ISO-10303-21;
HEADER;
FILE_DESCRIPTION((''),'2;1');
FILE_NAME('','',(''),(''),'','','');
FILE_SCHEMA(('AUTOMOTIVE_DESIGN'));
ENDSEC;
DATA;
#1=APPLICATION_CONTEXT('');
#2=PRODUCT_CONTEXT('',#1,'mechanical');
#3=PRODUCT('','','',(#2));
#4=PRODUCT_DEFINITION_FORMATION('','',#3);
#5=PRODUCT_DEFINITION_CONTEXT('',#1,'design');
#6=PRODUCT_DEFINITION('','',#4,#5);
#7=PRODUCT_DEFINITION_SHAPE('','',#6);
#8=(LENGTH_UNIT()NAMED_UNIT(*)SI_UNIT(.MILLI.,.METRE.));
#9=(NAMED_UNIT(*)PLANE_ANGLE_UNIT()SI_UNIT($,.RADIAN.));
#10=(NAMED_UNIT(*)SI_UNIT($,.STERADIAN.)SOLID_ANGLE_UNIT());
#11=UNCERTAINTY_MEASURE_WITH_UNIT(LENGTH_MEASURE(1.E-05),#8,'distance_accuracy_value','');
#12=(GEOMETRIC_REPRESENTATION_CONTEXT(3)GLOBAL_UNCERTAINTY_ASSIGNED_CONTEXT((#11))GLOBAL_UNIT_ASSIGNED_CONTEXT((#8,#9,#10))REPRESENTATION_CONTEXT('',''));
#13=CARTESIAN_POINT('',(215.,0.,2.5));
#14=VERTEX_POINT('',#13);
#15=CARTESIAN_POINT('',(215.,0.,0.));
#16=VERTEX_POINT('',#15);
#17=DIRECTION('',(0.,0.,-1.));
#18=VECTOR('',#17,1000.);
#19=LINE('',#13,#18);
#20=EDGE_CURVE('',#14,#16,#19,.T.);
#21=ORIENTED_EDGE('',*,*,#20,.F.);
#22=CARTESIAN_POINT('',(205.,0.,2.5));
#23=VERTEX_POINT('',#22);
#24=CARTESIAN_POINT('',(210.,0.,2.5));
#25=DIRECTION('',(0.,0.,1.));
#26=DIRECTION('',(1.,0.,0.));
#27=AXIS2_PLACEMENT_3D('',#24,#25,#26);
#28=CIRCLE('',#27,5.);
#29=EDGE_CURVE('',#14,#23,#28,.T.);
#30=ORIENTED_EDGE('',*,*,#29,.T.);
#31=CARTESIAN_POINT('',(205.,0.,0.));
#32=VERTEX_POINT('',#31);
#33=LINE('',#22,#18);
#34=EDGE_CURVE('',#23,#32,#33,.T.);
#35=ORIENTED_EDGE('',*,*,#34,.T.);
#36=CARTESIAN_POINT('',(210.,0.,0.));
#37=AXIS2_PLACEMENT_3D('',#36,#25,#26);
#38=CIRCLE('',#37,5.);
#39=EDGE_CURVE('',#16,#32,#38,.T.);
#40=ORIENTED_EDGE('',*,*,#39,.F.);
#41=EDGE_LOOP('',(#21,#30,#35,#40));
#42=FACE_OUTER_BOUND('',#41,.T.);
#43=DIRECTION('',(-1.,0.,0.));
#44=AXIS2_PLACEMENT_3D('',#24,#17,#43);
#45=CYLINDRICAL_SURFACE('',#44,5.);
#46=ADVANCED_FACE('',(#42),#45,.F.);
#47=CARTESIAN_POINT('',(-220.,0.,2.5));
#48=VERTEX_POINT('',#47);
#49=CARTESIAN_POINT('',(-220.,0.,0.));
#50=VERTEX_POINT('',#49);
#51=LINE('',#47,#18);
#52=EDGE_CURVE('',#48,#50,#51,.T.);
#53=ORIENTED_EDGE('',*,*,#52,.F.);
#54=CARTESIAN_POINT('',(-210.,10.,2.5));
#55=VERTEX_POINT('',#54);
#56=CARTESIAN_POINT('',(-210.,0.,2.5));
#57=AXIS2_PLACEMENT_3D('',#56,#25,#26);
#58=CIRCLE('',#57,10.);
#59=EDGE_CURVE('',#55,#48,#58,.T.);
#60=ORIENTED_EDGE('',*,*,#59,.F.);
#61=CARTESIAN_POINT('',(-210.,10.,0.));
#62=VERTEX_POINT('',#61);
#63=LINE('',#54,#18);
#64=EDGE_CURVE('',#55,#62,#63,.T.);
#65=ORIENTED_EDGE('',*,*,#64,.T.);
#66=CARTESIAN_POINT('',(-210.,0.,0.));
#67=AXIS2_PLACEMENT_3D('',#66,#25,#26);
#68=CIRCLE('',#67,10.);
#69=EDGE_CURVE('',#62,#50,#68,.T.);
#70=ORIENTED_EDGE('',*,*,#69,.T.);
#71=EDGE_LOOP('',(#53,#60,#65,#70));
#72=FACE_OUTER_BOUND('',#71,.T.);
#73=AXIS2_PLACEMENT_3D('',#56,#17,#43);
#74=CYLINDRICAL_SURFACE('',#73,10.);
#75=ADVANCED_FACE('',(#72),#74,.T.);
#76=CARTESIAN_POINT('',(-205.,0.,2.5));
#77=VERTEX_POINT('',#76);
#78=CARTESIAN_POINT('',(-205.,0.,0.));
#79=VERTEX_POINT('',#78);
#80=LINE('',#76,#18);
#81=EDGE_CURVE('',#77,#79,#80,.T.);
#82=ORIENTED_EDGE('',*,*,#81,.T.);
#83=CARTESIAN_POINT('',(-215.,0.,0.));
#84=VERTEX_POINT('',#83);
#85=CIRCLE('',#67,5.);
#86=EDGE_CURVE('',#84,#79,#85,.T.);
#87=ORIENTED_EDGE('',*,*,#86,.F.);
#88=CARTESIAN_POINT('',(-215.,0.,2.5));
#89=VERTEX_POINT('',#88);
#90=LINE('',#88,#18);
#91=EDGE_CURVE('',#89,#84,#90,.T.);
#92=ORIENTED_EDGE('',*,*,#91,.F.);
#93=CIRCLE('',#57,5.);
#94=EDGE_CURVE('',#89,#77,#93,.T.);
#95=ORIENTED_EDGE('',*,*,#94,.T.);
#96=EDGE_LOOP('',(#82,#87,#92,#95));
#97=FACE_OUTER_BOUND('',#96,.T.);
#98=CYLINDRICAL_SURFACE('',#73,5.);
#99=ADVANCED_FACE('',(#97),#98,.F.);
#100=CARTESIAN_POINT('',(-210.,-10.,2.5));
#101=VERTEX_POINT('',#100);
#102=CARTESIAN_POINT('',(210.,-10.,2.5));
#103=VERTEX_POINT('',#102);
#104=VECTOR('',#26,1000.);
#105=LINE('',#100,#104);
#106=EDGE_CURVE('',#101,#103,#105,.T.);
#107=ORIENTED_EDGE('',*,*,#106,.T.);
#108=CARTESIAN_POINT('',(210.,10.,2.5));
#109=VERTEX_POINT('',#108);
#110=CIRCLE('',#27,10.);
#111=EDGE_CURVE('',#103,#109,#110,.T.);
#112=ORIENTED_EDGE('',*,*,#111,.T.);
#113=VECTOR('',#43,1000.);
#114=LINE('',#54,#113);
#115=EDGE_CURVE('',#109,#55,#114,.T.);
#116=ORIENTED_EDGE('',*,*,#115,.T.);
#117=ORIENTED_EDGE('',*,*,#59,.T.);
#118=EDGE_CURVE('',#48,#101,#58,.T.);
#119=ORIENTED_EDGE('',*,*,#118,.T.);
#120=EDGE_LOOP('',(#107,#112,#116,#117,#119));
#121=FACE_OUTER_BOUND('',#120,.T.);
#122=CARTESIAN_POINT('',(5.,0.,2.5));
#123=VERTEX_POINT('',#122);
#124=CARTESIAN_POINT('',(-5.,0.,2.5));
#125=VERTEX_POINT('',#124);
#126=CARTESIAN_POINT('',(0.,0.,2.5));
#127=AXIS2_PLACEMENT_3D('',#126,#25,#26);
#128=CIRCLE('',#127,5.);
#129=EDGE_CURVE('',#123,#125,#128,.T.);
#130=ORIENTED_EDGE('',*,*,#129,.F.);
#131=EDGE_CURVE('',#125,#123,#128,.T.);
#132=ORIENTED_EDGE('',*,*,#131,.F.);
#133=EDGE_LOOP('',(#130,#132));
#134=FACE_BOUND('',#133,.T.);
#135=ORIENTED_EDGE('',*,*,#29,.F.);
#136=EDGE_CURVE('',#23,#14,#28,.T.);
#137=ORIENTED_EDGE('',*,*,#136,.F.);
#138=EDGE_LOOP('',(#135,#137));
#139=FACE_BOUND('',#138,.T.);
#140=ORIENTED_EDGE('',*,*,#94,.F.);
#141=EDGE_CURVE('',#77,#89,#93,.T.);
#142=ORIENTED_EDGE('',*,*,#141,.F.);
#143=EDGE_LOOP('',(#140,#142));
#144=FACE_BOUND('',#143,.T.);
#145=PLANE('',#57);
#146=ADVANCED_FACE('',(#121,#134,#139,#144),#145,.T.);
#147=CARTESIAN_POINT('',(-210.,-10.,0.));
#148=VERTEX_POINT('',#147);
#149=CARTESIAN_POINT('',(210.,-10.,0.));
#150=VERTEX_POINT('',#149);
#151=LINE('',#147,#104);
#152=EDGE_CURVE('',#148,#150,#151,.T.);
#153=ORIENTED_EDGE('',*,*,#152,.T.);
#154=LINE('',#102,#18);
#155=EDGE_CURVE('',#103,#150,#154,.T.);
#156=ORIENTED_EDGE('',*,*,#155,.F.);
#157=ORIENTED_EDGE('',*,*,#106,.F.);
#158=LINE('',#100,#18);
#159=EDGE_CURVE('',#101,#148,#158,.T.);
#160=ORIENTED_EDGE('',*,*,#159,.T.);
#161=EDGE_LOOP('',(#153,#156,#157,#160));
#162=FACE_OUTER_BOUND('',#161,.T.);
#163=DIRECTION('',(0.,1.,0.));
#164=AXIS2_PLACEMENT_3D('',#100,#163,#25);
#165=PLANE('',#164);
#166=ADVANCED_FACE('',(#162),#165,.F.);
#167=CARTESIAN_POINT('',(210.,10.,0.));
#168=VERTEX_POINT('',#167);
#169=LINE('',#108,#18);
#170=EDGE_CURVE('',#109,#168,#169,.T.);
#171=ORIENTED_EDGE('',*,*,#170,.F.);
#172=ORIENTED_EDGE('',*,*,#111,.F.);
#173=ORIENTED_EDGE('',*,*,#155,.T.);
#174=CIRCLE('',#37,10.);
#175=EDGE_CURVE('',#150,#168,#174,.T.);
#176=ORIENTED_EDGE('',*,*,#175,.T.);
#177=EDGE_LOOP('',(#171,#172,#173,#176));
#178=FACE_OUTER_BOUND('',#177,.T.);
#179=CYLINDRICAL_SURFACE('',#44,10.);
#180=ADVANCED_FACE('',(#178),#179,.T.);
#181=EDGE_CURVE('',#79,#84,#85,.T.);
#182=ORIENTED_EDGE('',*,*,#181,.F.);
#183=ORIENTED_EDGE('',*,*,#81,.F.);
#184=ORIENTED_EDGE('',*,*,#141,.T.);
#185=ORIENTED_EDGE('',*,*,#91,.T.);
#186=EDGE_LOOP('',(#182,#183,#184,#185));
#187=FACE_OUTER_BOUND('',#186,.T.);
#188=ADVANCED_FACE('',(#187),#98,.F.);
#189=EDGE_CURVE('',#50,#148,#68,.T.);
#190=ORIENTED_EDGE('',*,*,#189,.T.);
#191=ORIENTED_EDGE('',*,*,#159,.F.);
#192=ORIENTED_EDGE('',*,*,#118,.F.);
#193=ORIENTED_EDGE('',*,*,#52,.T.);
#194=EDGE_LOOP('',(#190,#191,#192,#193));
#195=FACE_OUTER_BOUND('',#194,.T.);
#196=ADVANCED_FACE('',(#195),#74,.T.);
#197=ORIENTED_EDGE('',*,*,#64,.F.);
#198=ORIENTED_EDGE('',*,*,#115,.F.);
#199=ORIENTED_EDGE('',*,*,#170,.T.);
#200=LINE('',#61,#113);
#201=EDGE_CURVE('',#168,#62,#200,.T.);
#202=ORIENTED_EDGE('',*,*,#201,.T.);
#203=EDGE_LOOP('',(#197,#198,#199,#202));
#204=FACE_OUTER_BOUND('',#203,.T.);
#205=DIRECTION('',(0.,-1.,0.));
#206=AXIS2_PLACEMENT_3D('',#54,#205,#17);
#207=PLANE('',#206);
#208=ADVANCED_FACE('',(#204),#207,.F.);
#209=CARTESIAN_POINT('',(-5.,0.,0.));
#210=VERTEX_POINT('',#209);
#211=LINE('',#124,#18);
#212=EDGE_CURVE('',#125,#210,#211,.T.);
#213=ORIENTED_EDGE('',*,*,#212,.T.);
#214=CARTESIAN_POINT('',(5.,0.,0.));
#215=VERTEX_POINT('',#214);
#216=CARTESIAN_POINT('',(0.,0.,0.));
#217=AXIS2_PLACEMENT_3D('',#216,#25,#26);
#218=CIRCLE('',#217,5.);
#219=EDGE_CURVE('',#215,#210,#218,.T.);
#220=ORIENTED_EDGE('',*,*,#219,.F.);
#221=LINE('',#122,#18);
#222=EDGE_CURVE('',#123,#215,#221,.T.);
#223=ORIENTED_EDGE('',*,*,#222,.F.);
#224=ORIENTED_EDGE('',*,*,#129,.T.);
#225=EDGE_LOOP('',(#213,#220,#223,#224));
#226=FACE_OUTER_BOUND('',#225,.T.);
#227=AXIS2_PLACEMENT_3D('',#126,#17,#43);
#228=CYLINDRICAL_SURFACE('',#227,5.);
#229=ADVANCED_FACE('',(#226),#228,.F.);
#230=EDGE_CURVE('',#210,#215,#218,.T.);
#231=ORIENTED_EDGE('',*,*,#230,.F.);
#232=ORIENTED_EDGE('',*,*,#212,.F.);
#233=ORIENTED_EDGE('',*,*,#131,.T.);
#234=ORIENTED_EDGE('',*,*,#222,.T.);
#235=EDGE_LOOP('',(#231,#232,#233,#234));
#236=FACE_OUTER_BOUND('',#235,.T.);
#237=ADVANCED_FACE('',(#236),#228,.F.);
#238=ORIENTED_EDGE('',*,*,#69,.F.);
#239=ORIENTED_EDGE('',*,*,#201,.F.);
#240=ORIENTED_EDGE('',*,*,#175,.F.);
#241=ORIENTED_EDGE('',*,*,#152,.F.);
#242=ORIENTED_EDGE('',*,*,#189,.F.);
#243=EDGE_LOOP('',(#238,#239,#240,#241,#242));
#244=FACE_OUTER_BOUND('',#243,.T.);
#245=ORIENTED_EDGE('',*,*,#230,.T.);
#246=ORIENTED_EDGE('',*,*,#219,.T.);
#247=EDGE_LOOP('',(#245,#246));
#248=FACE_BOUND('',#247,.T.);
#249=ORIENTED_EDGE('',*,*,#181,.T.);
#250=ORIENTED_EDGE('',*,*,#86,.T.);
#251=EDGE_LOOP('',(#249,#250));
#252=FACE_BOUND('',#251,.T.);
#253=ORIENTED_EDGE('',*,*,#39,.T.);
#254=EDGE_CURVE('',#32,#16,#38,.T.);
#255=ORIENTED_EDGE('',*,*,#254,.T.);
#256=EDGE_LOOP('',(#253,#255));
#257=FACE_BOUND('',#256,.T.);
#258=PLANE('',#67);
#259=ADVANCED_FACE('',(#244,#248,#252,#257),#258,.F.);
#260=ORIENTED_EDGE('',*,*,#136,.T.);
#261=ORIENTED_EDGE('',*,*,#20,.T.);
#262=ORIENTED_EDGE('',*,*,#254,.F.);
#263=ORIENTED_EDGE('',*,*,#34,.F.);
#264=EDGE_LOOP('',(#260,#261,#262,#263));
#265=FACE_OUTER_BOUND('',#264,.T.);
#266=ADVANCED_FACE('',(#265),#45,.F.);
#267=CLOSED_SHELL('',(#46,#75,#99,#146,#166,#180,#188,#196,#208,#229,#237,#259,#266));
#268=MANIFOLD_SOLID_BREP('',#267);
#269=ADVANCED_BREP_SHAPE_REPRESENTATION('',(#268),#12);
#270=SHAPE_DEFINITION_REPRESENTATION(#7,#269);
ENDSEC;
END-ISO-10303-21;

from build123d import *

# Parameters (mm, degrees)
SKETCH1_R           = 5
BOSS_EXTRUDE1_DEPTH = 2.5


with BuildPart() as part:
    # Sketch1 → Boss-Extrude1 (new body)
    with BuildSketch(Plane.XY):
        with BuildLine():
            Line((-210, 10), (210, 10))
            ThreePointArc((210, 10), (220, 0), (210, -10))
            Line((210, -10), (-210, -10))
            ThreePointArc((-210, -10), (-220, 0), (-210, 10))
        make_face()
        with Locations((-210, 0)):
            Circle(SKETCH1_R, mode=Mode.SUBTRACT)
        with Locations((210, 0)):
            Circle(SKETCH1_R, mode=Mode.SUBTRACT)
        Circle(SKETCH1_R, mode=Mode.SUBTRACT)
    extrude(amount=BOSS_EXTRUDE1_DEPTH)


solid = part.part
